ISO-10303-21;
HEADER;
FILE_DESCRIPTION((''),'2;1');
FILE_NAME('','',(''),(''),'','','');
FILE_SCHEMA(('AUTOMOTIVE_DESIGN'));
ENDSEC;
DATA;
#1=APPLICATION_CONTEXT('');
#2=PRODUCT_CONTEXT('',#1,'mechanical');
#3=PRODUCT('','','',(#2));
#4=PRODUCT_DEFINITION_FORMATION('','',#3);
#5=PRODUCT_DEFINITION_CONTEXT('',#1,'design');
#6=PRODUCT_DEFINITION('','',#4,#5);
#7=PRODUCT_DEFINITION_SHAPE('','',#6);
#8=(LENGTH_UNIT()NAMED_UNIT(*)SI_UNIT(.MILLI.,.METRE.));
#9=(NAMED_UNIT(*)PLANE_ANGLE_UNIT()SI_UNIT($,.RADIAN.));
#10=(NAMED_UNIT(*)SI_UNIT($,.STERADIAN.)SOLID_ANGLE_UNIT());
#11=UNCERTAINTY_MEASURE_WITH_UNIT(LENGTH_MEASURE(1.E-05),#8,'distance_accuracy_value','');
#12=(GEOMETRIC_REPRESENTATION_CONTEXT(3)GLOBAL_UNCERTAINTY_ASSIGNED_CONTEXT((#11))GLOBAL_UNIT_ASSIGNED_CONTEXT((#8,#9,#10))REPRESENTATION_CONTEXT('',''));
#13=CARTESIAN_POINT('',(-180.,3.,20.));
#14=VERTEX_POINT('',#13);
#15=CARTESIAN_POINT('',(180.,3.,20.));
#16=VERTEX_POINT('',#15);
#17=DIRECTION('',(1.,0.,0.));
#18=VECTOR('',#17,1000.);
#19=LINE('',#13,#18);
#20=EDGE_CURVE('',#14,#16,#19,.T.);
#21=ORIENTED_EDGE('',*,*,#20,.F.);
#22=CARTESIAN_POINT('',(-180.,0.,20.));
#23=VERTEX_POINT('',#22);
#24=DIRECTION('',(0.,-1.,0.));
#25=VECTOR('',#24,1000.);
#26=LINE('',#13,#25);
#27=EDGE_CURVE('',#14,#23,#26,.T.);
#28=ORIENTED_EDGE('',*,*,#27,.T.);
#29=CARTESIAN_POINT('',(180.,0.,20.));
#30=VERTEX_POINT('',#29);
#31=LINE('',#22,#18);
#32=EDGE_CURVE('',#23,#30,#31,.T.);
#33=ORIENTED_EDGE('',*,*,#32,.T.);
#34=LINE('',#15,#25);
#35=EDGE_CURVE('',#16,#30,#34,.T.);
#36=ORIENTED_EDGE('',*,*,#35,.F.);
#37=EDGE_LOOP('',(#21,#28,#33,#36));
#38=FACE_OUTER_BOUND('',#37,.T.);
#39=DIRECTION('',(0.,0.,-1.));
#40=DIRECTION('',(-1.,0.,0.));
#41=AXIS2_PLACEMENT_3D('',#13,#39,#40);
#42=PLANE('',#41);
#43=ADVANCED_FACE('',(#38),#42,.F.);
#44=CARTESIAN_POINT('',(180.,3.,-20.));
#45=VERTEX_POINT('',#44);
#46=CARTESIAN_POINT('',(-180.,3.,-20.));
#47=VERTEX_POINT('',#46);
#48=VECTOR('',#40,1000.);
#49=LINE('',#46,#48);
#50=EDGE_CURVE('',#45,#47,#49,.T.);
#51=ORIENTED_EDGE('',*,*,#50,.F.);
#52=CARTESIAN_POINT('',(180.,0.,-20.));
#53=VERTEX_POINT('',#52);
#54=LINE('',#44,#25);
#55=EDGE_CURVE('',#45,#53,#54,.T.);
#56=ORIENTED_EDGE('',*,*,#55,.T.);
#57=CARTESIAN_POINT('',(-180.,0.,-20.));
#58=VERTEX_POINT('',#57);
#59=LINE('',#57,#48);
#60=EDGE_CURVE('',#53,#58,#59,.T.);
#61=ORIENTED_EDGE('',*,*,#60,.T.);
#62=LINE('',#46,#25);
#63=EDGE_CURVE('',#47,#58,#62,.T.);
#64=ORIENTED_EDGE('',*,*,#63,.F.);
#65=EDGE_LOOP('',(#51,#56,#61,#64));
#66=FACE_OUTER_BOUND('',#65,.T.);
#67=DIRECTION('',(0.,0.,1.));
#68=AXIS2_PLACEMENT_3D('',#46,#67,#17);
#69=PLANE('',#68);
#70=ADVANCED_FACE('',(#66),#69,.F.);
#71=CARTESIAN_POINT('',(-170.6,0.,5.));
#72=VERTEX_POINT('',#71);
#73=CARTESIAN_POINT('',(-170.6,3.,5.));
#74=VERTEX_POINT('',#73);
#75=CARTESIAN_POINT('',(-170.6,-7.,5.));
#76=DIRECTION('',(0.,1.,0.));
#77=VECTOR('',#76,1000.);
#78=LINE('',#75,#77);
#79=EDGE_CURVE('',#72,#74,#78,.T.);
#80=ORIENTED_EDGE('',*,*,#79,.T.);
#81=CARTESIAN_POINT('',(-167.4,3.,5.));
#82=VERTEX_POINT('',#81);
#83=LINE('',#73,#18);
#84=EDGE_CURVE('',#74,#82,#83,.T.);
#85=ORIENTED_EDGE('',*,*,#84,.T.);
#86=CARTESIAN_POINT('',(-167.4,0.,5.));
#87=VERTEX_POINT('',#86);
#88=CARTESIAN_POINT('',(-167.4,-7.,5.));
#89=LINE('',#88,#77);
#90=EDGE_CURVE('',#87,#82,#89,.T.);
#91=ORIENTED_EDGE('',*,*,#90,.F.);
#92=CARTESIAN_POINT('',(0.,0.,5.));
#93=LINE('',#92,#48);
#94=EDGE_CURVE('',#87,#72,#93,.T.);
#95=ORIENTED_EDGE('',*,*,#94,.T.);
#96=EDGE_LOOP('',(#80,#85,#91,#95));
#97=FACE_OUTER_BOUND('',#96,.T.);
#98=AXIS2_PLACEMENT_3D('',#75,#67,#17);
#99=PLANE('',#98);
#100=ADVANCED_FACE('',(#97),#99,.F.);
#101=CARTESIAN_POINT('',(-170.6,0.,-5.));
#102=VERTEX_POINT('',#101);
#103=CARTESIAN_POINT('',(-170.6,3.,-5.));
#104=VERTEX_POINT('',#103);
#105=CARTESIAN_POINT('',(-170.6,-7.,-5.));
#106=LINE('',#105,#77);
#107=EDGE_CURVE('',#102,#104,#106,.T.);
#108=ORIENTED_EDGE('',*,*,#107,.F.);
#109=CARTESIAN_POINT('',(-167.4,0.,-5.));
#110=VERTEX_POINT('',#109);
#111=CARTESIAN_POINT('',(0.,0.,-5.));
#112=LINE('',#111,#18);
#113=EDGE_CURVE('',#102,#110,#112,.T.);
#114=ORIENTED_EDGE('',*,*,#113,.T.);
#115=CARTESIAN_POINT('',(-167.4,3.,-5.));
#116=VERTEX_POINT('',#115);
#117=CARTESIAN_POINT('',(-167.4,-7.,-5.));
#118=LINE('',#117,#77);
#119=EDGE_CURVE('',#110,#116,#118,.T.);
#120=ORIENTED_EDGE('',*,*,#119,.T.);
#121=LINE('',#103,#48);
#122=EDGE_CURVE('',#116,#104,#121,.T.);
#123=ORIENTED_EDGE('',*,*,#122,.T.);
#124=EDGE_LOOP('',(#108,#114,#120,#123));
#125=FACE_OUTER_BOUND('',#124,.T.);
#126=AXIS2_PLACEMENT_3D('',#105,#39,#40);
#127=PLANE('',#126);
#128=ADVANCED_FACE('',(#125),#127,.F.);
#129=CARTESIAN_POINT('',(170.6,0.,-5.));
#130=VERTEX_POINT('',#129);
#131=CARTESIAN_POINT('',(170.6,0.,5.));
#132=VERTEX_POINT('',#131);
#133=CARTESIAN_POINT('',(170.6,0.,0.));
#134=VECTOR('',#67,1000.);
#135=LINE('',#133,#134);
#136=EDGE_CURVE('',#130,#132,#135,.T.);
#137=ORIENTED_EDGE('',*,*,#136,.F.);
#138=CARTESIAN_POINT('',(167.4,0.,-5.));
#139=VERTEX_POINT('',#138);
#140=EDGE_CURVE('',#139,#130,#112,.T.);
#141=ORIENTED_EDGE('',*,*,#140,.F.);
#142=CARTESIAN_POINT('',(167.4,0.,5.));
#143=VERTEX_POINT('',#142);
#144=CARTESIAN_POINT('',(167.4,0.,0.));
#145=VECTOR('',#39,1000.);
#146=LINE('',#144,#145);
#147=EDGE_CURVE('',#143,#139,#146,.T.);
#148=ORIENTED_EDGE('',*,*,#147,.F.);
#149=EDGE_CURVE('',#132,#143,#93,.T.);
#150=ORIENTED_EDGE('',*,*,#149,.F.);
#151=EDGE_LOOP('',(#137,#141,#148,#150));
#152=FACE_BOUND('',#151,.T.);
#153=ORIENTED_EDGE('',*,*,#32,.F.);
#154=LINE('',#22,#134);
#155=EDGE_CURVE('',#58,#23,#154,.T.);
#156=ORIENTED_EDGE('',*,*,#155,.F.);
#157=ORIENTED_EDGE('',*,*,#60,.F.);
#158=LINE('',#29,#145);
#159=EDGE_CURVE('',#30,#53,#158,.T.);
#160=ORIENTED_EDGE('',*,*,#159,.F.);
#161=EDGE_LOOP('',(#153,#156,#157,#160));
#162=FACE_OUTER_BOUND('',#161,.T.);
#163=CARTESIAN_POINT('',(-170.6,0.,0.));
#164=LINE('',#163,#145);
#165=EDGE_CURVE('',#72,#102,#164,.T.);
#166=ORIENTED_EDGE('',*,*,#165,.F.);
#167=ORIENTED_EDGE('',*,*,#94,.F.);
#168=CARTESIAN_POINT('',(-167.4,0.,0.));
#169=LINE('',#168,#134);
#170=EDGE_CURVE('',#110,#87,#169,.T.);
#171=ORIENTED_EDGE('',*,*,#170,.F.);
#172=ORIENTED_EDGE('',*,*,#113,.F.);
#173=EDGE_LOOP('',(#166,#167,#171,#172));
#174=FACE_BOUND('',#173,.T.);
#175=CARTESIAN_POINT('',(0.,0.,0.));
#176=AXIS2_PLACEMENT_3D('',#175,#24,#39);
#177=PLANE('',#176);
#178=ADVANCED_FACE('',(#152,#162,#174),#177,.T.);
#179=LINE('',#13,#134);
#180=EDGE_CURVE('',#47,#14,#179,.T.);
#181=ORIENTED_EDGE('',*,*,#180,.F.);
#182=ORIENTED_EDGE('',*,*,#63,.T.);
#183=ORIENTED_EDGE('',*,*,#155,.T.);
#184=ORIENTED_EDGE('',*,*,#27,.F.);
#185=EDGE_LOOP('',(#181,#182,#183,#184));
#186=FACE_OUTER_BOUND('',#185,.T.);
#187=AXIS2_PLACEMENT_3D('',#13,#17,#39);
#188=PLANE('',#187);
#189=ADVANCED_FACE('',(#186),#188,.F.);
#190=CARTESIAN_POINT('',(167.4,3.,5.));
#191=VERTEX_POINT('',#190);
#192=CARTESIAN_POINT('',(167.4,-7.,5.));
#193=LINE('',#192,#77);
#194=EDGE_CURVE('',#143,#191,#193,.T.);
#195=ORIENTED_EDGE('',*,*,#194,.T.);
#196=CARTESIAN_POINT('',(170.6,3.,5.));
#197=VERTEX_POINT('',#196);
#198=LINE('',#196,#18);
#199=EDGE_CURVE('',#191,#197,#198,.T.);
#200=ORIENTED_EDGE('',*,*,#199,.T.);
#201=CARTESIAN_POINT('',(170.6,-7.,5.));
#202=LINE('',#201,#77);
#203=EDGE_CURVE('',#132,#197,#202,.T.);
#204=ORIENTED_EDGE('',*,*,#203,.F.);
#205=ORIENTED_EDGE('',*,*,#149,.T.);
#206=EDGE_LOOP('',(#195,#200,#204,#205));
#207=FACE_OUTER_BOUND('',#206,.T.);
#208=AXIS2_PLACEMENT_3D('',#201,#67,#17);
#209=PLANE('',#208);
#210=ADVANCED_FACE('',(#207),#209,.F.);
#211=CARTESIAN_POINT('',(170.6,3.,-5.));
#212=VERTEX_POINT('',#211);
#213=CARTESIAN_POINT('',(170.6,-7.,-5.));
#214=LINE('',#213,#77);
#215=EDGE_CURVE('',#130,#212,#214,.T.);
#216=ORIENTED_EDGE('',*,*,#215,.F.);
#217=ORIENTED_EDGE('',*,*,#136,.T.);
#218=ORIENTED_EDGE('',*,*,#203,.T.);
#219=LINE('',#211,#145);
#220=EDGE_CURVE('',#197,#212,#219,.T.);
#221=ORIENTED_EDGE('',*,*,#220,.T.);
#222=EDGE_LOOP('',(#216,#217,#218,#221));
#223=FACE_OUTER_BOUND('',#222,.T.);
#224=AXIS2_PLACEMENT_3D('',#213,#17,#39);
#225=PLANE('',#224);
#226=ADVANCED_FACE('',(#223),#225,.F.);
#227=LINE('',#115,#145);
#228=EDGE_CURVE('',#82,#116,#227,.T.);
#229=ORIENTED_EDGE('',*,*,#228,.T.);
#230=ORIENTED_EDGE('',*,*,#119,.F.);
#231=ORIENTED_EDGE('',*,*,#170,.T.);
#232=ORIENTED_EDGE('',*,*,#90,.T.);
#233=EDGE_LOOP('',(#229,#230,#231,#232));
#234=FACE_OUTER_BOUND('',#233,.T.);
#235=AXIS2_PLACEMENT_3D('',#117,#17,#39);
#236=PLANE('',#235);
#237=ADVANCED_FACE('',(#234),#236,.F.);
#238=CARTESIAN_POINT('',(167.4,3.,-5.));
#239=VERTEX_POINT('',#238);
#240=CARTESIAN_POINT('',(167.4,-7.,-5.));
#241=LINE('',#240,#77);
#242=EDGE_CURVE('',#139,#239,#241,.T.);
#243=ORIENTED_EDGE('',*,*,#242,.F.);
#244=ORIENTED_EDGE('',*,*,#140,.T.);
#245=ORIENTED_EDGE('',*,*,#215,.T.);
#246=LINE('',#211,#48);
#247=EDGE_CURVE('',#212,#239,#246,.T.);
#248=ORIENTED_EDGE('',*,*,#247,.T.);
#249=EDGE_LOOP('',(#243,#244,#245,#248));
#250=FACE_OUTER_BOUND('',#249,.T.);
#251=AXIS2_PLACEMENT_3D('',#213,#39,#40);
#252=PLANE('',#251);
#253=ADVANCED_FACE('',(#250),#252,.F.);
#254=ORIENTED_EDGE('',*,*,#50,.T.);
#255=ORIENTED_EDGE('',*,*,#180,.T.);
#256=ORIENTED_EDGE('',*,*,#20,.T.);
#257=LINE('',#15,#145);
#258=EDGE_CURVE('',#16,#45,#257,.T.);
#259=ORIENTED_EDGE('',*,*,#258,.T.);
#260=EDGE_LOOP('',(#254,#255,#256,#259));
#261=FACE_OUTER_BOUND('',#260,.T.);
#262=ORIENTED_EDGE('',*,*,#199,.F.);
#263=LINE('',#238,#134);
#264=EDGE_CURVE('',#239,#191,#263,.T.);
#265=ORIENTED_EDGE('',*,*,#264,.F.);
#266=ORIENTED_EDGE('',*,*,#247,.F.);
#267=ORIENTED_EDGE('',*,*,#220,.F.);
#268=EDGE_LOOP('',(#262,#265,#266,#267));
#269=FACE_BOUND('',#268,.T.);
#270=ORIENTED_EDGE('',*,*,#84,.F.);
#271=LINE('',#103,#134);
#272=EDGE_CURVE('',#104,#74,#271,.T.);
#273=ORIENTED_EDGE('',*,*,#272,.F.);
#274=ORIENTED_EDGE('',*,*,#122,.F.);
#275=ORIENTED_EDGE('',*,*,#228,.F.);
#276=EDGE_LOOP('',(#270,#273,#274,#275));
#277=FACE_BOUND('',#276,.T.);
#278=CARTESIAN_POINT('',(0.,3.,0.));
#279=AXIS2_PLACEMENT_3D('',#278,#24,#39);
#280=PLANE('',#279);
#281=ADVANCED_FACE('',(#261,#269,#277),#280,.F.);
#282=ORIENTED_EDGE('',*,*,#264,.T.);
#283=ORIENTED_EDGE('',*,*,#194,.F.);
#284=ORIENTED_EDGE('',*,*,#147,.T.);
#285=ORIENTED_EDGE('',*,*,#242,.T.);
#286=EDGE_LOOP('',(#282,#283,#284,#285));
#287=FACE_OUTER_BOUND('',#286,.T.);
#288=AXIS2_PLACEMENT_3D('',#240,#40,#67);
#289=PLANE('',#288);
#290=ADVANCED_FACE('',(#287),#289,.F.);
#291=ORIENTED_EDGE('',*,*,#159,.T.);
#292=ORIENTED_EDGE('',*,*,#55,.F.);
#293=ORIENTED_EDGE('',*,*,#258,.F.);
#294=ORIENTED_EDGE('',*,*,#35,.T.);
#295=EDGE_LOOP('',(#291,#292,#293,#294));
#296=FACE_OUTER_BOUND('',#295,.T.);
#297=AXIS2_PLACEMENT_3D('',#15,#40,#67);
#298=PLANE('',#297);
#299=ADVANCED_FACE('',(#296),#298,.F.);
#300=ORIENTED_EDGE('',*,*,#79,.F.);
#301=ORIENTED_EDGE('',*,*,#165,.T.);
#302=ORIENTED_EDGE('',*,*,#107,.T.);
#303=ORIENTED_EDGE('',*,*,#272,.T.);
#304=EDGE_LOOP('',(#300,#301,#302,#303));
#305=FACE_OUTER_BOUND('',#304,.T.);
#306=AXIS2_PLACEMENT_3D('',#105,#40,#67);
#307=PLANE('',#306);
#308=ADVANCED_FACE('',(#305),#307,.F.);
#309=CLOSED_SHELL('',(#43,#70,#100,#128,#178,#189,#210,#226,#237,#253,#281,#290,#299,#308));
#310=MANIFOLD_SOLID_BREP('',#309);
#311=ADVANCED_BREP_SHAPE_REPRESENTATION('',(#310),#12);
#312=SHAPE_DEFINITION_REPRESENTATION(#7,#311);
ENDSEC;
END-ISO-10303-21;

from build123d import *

# Parameters (mm, degrees)
SKETCH1_W           = 360
SKETCH1_H           = 40
BOSS_EXTRUDE1_DEPTH = 3
SKETCH2_W           = 3.2
SKETCH2_H           = 10
CUT_EXTRUDE1_DEPTH  = 10


with BuildPart() as part:
    # Sketch1 → Boss-Extrude1 (new body)
    with BuildSketch(Plane(origin=(0, 0, 0), x_dir=(1, 0, 0), z_dir=(0, 1, 0))):
        Rectangle(SKETCH1_W, SKETCH1_H)
    extrude(amount=BOSS_EXTRUDE1_DEPTH)

    # Sketch2 → Cut-Extrude1 (cut)
    with BuildSketch(Plane(origin=(0, 3, 0), x_dir=(1, 0, 0), z_dir=(0, 1, 0))):
        with Locations((-169, 0)):
            Rectangle(SKETCH2_W, SKETCH2_H)
        with Locations((169, 0)):
            Rectangle(SKETCH2_W, SKETCH2_H)
    extrude(amount=-CUT_EXTRUDE1_DEPTH, mode=Mode.SUBTRACT)


solid = part.part
